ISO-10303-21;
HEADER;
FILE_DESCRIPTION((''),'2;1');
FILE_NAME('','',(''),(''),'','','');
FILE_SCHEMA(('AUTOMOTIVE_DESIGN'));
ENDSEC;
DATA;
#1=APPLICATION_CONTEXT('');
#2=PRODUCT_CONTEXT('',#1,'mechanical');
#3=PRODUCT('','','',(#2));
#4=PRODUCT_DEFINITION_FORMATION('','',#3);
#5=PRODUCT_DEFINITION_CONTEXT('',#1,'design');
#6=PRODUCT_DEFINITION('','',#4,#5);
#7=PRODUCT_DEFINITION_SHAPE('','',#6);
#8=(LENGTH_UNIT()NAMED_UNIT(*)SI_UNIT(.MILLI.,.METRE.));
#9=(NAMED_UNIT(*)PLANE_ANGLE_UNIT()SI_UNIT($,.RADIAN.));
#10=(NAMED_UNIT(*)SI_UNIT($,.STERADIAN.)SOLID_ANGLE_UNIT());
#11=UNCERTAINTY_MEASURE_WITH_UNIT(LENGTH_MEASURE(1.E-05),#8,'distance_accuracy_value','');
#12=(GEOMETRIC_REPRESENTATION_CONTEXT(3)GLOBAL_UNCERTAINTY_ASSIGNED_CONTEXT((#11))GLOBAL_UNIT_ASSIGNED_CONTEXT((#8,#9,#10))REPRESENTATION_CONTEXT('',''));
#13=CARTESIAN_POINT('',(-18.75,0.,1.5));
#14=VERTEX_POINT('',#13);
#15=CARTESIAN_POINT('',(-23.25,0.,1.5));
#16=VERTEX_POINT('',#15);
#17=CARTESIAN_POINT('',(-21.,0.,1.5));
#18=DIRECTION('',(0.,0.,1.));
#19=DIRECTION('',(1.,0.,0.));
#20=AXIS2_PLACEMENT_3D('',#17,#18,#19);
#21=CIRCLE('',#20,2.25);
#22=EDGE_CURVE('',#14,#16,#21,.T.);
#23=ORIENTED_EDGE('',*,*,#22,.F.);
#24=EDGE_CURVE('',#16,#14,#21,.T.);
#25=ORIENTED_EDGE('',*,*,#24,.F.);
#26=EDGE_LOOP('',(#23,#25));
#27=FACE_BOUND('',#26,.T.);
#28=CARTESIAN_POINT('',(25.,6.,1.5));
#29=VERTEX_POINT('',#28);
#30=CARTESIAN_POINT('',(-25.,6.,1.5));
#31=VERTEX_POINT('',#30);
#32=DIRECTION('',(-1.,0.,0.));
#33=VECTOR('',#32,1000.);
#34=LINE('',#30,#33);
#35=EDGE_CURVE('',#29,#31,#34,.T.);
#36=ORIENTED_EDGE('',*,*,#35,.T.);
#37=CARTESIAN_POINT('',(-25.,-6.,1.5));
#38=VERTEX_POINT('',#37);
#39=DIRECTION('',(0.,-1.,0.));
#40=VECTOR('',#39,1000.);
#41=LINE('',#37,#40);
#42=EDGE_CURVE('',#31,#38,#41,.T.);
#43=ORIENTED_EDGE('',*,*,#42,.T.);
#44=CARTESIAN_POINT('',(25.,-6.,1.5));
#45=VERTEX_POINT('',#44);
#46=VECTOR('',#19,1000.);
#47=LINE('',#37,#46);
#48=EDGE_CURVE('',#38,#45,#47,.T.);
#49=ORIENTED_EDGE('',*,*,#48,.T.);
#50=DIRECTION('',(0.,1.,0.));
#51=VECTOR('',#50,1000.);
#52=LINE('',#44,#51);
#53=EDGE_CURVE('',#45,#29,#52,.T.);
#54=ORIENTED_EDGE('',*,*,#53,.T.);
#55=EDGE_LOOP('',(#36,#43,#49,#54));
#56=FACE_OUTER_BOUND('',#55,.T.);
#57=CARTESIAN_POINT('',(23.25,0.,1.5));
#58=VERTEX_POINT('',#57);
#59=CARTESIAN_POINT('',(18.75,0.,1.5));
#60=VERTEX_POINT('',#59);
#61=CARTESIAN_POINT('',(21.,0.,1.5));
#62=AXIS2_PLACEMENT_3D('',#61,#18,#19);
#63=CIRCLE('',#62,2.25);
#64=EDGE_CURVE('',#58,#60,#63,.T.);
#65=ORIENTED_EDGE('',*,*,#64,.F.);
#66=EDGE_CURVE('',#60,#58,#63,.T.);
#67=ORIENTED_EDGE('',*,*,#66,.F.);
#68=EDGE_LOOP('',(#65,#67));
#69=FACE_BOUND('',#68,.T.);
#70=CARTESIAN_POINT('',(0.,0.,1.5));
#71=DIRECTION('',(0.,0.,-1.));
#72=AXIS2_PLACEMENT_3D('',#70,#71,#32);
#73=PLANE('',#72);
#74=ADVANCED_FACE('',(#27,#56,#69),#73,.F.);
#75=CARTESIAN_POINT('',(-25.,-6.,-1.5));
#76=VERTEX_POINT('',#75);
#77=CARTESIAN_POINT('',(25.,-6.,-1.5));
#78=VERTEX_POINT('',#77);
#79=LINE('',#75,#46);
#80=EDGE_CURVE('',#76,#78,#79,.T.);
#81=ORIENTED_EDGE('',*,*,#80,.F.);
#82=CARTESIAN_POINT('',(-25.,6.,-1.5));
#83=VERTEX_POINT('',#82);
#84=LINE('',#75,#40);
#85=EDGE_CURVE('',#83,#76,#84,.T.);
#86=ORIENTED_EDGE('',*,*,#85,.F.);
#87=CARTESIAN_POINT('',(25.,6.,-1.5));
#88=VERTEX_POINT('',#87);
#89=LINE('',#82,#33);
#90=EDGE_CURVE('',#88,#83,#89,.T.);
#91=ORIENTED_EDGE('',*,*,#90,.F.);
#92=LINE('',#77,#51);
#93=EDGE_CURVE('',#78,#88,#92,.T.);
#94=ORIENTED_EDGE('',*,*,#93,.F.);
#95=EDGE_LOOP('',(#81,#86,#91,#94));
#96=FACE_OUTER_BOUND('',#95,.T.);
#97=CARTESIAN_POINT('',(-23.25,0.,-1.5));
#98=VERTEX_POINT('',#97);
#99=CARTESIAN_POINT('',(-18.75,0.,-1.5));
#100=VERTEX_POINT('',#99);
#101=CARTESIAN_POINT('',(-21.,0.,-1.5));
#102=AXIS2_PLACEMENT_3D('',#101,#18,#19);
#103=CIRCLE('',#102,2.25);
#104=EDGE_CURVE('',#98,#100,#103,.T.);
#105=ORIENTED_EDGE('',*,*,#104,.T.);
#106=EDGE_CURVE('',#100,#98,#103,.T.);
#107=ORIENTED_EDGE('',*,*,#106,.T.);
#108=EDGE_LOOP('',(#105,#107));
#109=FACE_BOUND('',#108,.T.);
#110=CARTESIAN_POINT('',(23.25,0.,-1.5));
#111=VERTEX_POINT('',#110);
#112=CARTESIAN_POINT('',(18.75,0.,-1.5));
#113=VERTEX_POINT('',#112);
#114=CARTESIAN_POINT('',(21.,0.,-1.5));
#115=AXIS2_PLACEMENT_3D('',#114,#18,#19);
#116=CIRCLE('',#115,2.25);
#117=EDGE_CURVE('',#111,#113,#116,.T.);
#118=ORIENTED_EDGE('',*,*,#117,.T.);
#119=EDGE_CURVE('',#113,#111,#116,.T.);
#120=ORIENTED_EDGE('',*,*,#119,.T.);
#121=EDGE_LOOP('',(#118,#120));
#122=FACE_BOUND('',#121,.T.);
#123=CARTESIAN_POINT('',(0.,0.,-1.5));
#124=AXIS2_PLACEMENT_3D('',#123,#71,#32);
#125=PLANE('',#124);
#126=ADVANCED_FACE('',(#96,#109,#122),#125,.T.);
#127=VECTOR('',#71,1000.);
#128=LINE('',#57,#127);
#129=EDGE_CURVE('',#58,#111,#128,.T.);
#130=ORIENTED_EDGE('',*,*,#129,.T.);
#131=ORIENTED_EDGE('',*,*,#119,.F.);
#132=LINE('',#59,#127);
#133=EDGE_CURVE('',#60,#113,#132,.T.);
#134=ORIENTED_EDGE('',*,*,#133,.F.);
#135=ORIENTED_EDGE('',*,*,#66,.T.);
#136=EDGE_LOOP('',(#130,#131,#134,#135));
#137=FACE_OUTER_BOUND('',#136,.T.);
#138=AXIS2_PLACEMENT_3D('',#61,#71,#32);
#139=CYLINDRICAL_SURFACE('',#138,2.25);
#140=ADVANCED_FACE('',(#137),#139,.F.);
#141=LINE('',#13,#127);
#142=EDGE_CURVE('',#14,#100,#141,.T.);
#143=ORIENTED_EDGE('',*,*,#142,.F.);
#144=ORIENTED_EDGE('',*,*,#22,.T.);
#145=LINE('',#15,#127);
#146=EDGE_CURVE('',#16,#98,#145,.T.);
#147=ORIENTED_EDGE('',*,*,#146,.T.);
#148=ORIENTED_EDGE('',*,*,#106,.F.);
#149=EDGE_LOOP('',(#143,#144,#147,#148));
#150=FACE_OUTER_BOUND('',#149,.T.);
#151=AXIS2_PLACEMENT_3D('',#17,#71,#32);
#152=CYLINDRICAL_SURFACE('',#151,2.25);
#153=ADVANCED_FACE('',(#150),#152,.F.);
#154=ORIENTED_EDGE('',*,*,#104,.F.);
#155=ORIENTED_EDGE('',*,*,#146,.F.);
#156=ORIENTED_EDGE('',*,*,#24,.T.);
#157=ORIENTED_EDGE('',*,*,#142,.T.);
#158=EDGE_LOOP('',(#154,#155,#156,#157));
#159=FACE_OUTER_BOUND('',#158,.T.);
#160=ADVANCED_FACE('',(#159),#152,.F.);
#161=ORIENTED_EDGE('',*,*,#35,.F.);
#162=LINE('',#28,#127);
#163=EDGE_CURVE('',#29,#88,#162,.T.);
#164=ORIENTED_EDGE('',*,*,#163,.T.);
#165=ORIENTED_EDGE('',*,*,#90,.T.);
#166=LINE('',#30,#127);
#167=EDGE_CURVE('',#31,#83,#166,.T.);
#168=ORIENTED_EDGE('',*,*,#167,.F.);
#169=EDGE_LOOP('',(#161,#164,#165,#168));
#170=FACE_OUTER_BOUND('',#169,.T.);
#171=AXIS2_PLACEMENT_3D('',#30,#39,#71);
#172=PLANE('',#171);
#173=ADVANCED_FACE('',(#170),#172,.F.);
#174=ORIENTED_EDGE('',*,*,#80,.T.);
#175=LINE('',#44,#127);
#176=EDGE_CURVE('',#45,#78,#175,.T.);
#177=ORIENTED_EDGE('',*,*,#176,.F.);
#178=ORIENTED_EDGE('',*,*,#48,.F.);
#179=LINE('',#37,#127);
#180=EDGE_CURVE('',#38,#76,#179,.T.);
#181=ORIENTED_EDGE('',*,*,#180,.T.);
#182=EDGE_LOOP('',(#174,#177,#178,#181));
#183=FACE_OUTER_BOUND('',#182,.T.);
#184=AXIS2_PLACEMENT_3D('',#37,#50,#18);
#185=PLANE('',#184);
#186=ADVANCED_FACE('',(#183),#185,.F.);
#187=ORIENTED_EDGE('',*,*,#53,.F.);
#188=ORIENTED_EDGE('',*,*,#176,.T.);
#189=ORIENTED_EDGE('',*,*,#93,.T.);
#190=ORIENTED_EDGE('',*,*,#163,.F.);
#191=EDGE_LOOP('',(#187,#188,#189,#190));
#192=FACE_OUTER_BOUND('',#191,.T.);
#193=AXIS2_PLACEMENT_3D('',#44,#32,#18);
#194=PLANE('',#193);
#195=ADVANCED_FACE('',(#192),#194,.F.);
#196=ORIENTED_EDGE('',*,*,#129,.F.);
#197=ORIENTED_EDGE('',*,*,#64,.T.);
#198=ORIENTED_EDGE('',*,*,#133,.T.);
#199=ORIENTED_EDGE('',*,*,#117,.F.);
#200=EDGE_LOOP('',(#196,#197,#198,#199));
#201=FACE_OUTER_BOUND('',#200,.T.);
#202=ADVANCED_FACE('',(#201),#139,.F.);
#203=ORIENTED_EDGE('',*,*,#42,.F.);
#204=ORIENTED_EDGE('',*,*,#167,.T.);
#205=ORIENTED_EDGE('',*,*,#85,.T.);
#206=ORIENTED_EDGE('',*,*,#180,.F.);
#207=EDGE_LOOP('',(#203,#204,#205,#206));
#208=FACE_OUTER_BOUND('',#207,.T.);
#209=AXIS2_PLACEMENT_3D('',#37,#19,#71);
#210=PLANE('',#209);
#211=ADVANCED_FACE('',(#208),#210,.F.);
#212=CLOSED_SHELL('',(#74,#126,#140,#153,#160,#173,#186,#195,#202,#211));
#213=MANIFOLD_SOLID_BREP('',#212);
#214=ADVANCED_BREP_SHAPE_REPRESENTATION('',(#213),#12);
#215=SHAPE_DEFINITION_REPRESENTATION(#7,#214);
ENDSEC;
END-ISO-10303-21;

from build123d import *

# Parameters (mm, degrees)
SKETCH_1_W      = 50
SKETCH_1_H      = 12
SKETCH_1_R      = 2.25
EXTRUDE_1_DEPTH = 1.5


with BuildPart() as part:
    # 草图1 → 凸台-拉伸1 (new, symmetric)
    with BuildSketch(Plane.XY):
        Rectangle(SKETCH_1_W, SKETCH_1_H)
        with Locations((-21, 0)):
            Circle(SKETCH_1_R, mode=Mode.SUBTRACT)
        with Locations((21, 0)):
            Circle(SKETCH_1_R, mode=Mode.SUBTRACT)
    extrude(amount=EXTRUDE_1_DEPTH, both=True)


solid = part.part
